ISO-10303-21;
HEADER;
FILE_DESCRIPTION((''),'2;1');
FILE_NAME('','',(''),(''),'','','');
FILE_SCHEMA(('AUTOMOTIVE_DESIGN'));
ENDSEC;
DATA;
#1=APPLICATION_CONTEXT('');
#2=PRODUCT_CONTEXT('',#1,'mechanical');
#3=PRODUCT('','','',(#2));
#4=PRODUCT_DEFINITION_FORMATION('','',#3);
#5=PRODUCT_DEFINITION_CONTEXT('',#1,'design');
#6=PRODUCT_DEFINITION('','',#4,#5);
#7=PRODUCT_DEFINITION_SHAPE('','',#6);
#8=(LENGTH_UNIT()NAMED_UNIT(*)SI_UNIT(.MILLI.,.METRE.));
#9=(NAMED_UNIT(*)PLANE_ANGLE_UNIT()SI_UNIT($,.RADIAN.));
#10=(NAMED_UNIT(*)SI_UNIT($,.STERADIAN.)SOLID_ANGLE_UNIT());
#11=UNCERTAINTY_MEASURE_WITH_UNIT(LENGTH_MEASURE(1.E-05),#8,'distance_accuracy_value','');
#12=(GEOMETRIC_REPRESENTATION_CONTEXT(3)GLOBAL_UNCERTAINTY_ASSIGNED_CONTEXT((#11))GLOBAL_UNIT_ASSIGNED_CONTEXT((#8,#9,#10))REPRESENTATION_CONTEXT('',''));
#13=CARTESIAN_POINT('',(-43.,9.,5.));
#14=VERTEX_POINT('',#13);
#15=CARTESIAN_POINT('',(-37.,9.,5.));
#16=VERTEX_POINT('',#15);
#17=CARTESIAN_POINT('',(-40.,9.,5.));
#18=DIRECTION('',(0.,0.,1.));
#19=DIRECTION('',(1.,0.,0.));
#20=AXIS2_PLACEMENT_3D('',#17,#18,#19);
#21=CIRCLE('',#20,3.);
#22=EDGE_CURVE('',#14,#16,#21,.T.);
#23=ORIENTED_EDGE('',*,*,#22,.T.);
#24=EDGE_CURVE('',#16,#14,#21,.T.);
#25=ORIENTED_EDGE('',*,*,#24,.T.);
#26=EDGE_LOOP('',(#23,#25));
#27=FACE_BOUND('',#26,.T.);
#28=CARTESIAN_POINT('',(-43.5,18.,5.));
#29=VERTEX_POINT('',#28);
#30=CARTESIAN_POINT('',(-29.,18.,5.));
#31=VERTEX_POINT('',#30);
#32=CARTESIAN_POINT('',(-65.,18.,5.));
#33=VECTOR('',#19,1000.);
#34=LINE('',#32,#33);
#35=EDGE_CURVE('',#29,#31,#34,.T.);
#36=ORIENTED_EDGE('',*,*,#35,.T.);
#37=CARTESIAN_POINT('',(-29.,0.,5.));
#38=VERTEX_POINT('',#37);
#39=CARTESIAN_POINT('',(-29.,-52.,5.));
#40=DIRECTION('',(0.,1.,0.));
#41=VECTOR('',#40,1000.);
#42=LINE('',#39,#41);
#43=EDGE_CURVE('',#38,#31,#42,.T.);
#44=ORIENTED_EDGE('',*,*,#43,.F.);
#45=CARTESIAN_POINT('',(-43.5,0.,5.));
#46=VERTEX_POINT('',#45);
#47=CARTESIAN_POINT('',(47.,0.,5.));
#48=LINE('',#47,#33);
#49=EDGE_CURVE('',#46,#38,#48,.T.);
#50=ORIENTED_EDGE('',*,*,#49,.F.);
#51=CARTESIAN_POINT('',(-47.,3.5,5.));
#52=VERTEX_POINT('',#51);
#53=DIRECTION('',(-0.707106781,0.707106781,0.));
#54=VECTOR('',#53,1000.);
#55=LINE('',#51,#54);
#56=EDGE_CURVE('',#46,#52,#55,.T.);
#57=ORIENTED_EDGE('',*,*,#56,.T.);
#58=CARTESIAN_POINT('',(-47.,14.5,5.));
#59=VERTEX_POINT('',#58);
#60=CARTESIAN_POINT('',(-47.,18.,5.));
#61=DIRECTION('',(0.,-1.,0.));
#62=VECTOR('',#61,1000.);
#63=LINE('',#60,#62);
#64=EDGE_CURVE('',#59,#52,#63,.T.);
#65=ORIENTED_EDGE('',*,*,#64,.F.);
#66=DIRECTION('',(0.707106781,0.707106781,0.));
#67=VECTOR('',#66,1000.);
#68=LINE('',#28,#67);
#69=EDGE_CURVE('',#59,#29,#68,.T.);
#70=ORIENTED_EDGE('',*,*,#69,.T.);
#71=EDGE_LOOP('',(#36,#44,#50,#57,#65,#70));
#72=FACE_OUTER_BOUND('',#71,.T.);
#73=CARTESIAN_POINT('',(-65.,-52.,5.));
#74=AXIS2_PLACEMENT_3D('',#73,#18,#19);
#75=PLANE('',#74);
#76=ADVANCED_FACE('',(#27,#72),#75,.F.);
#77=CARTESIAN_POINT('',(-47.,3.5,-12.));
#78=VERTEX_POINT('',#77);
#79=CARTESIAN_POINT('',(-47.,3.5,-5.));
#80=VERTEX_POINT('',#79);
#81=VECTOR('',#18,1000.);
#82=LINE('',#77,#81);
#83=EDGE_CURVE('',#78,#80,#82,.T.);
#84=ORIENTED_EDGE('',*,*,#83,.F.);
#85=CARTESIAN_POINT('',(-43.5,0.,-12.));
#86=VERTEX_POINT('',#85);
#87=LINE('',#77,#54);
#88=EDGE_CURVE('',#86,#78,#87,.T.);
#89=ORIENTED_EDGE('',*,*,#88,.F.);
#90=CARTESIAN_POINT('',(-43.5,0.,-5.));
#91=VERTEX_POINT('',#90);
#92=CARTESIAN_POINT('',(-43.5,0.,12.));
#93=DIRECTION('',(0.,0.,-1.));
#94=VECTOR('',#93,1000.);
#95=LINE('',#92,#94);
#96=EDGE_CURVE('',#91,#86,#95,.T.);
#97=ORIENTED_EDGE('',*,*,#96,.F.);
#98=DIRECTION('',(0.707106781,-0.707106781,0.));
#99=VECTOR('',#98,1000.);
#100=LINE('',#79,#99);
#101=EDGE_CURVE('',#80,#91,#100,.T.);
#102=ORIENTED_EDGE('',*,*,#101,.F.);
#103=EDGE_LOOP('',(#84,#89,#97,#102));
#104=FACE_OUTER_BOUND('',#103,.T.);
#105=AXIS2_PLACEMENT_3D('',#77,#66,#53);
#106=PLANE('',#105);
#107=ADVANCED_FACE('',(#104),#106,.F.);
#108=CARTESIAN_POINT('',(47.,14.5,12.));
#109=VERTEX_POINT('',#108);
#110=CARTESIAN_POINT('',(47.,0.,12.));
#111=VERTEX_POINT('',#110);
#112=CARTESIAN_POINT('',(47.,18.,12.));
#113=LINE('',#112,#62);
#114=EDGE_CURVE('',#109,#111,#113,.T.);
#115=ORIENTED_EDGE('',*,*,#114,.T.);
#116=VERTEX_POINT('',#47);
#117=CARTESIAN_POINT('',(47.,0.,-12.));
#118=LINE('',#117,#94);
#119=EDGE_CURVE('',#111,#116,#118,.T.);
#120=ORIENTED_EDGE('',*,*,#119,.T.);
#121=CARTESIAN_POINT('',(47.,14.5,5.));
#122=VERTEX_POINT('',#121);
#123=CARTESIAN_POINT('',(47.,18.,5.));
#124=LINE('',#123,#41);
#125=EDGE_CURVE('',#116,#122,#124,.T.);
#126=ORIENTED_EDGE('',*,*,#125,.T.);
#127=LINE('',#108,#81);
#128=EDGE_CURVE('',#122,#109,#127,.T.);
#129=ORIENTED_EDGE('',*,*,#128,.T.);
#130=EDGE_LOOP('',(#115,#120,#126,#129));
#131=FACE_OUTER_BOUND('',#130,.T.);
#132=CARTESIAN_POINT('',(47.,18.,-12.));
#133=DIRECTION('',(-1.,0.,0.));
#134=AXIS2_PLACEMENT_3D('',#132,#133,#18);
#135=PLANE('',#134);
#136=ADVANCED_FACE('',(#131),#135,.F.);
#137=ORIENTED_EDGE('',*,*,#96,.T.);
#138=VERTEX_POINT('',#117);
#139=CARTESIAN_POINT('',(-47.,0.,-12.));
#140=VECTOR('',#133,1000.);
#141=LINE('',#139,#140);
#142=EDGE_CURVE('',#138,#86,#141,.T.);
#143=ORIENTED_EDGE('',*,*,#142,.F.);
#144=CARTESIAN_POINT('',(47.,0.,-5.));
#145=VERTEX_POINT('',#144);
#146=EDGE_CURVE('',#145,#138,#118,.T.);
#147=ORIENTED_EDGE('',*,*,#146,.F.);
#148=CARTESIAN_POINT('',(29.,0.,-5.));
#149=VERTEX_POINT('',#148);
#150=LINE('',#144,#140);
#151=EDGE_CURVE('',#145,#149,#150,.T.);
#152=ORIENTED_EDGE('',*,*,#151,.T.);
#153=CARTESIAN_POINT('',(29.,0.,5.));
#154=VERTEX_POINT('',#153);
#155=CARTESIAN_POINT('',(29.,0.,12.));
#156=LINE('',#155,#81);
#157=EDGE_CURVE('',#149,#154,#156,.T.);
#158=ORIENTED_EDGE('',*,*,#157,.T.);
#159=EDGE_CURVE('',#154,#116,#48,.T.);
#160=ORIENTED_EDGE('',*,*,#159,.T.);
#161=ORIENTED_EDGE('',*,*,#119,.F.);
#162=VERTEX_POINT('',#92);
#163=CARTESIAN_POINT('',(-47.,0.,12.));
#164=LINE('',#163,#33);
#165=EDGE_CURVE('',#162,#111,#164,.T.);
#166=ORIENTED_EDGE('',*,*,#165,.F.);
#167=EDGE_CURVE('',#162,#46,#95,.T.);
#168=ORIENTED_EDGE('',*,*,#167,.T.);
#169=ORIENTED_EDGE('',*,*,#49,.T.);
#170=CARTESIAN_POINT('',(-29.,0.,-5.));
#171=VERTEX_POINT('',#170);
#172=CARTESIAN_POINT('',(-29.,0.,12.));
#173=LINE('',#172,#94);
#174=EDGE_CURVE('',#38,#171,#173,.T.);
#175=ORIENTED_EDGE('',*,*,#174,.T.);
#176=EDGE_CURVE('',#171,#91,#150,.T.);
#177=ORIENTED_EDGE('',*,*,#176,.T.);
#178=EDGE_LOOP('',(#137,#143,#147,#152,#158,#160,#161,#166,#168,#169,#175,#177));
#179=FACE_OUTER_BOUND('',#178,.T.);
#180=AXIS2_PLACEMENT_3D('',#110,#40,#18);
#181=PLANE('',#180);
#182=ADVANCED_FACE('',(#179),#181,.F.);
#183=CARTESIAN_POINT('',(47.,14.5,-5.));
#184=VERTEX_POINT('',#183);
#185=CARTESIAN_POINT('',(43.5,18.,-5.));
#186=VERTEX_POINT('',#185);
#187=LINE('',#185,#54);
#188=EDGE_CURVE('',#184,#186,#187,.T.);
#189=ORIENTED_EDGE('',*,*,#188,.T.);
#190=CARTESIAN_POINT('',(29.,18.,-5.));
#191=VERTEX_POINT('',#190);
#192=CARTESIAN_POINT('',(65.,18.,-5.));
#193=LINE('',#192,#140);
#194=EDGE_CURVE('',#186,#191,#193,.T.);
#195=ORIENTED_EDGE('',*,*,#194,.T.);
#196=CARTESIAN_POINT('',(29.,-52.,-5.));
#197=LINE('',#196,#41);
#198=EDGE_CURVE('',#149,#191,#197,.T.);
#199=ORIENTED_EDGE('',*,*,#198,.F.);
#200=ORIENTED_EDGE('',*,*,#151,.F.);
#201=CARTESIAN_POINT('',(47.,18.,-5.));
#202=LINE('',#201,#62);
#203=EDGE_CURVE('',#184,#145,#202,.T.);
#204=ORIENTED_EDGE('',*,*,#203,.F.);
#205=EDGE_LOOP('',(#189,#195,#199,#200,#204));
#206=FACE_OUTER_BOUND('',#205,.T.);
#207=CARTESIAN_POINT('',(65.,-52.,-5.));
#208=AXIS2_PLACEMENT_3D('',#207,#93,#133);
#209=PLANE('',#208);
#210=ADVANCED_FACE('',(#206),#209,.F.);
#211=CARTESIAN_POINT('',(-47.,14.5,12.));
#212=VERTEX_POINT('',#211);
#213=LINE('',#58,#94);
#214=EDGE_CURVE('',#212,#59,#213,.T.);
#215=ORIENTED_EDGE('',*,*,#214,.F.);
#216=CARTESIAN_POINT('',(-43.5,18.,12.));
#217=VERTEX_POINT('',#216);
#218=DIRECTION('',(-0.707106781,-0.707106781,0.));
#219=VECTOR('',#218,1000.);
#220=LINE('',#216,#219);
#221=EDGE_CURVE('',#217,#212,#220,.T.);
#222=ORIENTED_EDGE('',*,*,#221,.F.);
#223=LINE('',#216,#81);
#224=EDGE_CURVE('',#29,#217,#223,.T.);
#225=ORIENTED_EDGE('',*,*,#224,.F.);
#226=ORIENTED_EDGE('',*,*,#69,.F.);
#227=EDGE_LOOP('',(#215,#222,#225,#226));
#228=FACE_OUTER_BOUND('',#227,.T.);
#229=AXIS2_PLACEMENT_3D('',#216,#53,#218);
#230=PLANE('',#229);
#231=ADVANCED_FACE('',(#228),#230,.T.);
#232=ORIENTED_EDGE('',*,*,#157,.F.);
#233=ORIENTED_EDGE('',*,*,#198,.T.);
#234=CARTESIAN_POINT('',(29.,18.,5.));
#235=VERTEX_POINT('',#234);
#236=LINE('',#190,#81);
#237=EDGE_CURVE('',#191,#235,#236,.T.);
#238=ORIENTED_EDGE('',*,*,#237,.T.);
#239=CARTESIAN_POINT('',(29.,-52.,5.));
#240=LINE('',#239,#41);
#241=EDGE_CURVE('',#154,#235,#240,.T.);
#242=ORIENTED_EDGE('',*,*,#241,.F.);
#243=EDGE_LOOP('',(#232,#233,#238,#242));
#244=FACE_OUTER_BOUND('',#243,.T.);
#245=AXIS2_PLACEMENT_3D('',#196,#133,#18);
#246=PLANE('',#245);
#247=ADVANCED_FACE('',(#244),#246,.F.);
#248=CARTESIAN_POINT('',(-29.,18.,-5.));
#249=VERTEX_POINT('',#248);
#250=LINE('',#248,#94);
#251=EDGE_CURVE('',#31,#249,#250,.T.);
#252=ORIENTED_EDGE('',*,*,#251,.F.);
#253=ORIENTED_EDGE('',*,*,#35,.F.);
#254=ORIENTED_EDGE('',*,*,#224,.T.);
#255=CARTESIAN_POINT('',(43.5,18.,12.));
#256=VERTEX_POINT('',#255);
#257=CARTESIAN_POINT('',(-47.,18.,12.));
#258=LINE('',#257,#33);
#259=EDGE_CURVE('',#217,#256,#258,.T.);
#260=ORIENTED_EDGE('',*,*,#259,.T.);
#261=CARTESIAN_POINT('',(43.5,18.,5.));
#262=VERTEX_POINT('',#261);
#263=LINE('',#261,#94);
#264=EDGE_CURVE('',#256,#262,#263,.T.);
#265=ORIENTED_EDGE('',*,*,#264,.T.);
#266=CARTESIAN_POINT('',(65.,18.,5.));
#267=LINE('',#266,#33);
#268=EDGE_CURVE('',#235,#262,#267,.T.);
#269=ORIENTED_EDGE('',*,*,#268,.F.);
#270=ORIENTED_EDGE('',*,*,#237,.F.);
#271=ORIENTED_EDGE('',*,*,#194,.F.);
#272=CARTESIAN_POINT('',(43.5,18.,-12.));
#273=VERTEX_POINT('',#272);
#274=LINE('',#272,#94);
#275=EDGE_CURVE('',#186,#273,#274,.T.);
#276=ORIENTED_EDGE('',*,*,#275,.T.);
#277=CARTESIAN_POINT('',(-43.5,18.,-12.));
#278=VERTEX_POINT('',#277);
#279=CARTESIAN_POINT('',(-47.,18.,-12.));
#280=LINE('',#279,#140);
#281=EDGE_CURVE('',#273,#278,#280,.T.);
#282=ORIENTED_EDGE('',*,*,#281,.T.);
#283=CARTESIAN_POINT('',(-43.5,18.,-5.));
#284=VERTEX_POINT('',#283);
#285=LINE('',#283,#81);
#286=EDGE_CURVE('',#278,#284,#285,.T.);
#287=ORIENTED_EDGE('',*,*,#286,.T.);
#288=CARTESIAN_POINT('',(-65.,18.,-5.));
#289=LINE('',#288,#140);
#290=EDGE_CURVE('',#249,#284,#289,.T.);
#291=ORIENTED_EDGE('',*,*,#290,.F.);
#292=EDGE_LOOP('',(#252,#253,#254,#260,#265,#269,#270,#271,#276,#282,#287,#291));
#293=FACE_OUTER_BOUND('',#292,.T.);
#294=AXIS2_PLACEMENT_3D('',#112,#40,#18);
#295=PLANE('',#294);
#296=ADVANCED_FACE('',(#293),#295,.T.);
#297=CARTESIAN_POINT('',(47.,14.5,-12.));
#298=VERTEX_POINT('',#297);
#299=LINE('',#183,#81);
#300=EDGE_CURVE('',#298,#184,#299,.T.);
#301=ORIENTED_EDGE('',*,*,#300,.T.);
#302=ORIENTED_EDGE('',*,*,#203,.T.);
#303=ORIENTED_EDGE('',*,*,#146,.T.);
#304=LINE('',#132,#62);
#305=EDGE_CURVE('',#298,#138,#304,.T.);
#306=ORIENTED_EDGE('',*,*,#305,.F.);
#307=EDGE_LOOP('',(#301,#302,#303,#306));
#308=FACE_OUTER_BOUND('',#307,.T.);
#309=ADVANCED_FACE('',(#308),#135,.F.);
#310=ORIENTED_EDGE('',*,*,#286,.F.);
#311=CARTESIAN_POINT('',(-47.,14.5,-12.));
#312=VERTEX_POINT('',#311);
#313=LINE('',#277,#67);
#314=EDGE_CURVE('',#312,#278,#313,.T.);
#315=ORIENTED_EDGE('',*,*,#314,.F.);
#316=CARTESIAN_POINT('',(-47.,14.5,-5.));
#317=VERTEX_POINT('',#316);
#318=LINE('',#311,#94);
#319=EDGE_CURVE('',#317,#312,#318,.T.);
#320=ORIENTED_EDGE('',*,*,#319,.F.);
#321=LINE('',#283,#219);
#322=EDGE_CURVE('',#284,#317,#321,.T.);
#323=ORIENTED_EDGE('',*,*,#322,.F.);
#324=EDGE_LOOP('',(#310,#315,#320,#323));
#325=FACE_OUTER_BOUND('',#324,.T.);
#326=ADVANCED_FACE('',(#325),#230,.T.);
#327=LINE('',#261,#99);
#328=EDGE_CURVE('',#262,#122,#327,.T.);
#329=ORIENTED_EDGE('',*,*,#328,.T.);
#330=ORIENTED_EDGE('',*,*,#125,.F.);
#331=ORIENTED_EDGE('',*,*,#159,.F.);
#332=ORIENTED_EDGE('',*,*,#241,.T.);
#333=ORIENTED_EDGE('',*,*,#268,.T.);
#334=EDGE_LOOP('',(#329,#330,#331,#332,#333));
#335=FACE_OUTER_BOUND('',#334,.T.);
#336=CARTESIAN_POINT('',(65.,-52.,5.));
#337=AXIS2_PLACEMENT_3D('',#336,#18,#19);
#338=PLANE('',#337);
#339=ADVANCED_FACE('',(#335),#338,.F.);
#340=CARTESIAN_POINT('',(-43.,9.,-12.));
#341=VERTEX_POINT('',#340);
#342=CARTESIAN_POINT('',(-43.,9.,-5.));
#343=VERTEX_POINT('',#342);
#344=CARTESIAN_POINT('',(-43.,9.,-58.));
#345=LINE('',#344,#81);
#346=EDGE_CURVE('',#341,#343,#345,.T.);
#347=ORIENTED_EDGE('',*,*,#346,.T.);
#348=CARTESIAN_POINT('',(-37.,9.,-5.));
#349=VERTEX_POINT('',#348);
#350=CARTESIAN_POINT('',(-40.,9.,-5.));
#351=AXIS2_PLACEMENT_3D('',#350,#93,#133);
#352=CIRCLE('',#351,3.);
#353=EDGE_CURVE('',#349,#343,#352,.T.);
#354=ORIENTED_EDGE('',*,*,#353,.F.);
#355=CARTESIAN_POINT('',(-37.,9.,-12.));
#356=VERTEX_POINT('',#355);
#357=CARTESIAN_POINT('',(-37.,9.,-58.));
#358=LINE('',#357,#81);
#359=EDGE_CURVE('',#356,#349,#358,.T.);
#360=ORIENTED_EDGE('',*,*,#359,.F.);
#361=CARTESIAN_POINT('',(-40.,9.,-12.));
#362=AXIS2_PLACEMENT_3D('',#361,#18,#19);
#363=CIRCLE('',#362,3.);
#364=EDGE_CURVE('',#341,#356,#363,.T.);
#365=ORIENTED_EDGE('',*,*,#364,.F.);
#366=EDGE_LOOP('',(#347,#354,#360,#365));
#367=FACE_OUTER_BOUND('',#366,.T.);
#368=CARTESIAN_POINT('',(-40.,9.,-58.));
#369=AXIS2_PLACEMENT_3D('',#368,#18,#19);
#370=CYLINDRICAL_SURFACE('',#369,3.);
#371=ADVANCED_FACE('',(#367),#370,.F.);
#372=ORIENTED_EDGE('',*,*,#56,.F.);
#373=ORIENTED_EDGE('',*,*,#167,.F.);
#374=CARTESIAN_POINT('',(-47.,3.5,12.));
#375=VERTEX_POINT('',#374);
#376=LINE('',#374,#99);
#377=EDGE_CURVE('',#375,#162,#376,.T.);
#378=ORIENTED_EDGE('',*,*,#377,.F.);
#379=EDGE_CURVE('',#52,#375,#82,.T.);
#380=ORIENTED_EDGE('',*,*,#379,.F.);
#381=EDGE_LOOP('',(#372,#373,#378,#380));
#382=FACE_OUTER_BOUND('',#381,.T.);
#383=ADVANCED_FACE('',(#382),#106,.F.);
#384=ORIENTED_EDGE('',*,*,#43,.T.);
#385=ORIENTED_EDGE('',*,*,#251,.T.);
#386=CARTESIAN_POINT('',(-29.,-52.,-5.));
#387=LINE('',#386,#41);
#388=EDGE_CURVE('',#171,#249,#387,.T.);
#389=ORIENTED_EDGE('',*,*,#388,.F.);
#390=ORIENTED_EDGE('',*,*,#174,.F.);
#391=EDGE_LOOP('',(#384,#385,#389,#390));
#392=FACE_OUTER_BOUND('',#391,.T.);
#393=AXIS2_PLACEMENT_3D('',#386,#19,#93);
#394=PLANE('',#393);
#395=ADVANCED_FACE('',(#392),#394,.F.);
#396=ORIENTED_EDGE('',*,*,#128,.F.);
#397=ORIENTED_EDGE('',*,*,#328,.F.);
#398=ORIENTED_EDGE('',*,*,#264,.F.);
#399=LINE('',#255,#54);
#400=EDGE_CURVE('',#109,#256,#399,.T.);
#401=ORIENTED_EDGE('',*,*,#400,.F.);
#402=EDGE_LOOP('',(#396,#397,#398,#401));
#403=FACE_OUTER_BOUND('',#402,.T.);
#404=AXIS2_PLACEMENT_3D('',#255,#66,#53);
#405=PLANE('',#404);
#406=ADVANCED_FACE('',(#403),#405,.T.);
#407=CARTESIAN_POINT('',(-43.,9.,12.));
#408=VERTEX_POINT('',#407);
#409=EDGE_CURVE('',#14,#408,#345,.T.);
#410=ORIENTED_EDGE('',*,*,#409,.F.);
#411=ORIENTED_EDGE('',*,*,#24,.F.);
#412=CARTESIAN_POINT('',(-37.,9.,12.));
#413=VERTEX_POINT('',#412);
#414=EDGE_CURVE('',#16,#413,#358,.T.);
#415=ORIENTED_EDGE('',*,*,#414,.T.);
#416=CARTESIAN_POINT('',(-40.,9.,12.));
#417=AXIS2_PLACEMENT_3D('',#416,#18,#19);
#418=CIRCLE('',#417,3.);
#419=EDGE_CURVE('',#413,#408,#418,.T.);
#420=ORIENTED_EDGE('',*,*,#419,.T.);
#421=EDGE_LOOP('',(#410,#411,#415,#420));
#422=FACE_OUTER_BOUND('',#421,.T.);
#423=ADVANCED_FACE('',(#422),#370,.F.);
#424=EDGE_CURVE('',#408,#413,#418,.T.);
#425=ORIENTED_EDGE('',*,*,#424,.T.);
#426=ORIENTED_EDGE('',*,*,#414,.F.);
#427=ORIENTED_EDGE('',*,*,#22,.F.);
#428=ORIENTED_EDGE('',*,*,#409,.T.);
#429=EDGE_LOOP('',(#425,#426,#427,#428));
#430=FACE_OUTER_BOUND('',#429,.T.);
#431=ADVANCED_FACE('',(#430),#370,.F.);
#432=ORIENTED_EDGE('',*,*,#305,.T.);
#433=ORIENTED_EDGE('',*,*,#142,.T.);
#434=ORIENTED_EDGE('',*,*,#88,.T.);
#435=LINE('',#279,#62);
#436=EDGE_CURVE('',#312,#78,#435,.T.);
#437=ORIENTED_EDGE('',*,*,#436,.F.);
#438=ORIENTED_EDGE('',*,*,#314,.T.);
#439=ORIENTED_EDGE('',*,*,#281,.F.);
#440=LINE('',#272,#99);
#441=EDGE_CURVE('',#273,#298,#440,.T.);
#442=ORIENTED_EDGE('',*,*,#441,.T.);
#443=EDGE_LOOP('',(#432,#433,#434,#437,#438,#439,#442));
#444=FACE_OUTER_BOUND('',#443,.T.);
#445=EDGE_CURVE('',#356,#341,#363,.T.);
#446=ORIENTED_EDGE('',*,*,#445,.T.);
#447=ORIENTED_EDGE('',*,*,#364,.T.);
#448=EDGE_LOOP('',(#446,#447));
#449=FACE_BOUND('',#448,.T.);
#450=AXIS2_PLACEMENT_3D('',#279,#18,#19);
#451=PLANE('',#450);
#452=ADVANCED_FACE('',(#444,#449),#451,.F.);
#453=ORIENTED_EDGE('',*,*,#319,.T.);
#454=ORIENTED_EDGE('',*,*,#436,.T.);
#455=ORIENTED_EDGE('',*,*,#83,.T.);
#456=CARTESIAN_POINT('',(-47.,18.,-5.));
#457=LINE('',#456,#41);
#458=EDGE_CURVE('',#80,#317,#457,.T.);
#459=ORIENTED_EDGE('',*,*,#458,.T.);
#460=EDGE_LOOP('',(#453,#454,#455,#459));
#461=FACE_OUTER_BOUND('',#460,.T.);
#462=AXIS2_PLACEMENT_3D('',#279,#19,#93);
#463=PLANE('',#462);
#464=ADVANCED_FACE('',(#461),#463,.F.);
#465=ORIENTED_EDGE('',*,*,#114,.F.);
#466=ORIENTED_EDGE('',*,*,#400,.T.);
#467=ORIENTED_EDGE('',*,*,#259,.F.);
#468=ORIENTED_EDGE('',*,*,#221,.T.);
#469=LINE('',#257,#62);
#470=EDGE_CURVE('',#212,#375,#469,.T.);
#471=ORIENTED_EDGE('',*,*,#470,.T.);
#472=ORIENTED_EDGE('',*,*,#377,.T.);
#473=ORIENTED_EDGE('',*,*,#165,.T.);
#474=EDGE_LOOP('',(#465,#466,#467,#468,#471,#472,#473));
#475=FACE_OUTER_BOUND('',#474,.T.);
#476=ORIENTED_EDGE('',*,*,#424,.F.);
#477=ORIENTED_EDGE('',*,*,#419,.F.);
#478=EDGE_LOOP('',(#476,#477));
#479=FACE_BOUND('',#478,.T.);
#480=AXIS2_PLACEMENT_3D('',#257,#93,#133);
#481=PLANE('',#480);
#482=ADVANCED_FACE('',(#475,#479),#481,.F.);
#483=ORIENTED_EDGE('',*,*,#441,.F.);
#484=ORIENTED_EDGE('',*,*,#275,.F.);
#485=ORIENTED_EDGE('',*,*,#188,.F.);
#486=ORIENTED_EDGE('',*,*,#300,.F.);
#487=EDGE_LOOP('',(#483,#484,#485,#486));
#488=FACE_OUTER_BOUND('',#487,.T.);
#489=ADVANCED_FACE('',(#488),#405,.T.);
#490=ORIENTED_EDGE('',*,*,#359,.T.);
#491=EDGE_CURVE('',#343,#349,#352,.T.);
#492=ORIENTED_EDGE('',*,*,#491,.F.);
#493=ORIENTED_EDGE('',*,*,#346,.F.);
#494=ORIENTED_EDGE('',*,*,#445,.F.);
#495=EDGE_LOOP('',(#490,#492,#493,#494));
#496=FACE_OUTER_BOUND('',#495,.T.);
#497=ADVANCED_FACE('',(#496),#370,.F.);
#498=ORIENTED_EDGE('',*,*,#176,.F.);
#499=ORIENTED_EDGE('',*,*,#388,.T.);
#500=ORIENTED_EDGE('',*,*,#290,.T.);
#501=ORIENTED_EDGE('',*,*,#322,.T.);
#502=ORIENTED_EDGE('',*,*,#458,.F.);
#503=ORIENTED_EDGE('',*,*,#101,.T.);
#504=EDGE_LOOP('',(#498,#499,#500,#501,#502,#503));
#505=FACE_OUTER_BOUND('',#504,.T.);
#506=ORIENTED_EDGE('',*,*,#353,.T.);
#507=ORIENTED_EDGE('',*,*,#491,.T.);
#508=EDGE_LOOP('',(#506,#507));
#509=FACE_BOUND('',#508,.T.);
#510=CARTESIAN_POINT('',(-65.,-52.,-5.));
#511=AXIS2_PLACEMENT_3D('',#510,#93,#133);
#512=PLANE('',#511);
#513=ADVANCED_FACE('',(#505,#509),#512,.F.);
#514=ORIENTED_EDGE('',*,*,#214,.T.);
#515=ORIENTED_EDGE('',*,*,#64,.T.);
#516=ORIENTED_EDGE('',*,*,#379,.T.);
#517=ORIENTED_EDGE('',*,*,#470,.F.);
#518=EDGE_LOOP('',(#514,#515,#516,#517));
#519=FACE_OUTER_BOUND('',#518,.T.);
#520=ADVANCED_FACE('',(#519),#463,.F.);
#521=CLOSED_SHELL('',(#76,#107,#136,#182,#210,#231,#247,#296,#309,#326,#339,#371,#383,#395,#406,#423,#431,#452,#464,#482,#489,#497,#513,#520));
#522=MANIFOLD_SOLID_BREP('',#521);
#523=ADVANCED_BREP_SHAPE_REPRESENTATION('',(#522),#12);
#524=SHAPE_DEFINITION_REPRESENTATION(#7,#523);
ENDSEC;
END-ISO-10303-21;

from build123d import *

# Parameters (mm, degrees)
SKETCH1_W           = 94
SKETCH1_H           = 24
BOSS_EXTRUDE1_DEPTH = 18
SKETCH2_W           = 36
SKETCH2_H           = 10
CUT_EXTRUDE1_DEPTH  = 70
CHAMFER1_SIZE       = 3.5
CHAMFER2_SIZE       = 3.5
SKETCH3_R           = 3
CUT_EXTRUDE2_DEPTH  = 70


with BuildPart() as part:
    # Sketch1 → Boss-Extrude1 (new body)
    with BuildSketch(Plane(origin=(0, 0, 0), x_dir=(1, 0, 0), z_dir=(0, 1, 0))):
        Rectangle(SKETCH1_W, SKETCH1_H)
    extrude(amount=BOSS_EXTRUDE1_DEPTH)

    # Sketch2 → Cut-Extrude1 (cut)
    with BuildSketch(Plane(origin=(0, 18, 0), x_dir=(1, 0, 0), z_dir=(0, 1, 0))):
        with Locations((-47, 0)):
            Rectangle(SKETCH2_W, SKETCH2_H)
        with Locations((47, 0)):
            Rectangle(SKETCH2_W, SKETCH2_H)
    extrude(amount=-CUT_EXTRUDE1_DEPTH, mode=Mode.SUBTRACT)

    # Chamfer1
    chamfer1_edges = [part.edges().sort_by_distance(p)[0] for p in [
        (47, 18, -8.5),
        (47, 18, 8.5),
    ]]
    chamfer(chamfer1_edges, length=CHAMFER1_SIZE)

    # Chamfer2
    chamfer2_edges = [part.edges().sort_by_distance(p)[0] for p in [
        (-47, 18, -8.5),
        (-47, 0, 8.5),
        (-47, 18, 8.5),
        (-47, 0, -8.5),
    ]]
    chamfer(chamfer2_edges, length=CHAMFER2_SIZE)

    # Sketch3 → Cut-Extrude2 (cut)
    with BuildSketch(Plane.XY.offset(12)):
        with Locations((-40, 9)):
            Circle(SKETCH3_R)
    extrude(amount=-CUT_EXTRUDE2_DEPTH, mode=Mode.SUBTRACT)


solid = part.part
